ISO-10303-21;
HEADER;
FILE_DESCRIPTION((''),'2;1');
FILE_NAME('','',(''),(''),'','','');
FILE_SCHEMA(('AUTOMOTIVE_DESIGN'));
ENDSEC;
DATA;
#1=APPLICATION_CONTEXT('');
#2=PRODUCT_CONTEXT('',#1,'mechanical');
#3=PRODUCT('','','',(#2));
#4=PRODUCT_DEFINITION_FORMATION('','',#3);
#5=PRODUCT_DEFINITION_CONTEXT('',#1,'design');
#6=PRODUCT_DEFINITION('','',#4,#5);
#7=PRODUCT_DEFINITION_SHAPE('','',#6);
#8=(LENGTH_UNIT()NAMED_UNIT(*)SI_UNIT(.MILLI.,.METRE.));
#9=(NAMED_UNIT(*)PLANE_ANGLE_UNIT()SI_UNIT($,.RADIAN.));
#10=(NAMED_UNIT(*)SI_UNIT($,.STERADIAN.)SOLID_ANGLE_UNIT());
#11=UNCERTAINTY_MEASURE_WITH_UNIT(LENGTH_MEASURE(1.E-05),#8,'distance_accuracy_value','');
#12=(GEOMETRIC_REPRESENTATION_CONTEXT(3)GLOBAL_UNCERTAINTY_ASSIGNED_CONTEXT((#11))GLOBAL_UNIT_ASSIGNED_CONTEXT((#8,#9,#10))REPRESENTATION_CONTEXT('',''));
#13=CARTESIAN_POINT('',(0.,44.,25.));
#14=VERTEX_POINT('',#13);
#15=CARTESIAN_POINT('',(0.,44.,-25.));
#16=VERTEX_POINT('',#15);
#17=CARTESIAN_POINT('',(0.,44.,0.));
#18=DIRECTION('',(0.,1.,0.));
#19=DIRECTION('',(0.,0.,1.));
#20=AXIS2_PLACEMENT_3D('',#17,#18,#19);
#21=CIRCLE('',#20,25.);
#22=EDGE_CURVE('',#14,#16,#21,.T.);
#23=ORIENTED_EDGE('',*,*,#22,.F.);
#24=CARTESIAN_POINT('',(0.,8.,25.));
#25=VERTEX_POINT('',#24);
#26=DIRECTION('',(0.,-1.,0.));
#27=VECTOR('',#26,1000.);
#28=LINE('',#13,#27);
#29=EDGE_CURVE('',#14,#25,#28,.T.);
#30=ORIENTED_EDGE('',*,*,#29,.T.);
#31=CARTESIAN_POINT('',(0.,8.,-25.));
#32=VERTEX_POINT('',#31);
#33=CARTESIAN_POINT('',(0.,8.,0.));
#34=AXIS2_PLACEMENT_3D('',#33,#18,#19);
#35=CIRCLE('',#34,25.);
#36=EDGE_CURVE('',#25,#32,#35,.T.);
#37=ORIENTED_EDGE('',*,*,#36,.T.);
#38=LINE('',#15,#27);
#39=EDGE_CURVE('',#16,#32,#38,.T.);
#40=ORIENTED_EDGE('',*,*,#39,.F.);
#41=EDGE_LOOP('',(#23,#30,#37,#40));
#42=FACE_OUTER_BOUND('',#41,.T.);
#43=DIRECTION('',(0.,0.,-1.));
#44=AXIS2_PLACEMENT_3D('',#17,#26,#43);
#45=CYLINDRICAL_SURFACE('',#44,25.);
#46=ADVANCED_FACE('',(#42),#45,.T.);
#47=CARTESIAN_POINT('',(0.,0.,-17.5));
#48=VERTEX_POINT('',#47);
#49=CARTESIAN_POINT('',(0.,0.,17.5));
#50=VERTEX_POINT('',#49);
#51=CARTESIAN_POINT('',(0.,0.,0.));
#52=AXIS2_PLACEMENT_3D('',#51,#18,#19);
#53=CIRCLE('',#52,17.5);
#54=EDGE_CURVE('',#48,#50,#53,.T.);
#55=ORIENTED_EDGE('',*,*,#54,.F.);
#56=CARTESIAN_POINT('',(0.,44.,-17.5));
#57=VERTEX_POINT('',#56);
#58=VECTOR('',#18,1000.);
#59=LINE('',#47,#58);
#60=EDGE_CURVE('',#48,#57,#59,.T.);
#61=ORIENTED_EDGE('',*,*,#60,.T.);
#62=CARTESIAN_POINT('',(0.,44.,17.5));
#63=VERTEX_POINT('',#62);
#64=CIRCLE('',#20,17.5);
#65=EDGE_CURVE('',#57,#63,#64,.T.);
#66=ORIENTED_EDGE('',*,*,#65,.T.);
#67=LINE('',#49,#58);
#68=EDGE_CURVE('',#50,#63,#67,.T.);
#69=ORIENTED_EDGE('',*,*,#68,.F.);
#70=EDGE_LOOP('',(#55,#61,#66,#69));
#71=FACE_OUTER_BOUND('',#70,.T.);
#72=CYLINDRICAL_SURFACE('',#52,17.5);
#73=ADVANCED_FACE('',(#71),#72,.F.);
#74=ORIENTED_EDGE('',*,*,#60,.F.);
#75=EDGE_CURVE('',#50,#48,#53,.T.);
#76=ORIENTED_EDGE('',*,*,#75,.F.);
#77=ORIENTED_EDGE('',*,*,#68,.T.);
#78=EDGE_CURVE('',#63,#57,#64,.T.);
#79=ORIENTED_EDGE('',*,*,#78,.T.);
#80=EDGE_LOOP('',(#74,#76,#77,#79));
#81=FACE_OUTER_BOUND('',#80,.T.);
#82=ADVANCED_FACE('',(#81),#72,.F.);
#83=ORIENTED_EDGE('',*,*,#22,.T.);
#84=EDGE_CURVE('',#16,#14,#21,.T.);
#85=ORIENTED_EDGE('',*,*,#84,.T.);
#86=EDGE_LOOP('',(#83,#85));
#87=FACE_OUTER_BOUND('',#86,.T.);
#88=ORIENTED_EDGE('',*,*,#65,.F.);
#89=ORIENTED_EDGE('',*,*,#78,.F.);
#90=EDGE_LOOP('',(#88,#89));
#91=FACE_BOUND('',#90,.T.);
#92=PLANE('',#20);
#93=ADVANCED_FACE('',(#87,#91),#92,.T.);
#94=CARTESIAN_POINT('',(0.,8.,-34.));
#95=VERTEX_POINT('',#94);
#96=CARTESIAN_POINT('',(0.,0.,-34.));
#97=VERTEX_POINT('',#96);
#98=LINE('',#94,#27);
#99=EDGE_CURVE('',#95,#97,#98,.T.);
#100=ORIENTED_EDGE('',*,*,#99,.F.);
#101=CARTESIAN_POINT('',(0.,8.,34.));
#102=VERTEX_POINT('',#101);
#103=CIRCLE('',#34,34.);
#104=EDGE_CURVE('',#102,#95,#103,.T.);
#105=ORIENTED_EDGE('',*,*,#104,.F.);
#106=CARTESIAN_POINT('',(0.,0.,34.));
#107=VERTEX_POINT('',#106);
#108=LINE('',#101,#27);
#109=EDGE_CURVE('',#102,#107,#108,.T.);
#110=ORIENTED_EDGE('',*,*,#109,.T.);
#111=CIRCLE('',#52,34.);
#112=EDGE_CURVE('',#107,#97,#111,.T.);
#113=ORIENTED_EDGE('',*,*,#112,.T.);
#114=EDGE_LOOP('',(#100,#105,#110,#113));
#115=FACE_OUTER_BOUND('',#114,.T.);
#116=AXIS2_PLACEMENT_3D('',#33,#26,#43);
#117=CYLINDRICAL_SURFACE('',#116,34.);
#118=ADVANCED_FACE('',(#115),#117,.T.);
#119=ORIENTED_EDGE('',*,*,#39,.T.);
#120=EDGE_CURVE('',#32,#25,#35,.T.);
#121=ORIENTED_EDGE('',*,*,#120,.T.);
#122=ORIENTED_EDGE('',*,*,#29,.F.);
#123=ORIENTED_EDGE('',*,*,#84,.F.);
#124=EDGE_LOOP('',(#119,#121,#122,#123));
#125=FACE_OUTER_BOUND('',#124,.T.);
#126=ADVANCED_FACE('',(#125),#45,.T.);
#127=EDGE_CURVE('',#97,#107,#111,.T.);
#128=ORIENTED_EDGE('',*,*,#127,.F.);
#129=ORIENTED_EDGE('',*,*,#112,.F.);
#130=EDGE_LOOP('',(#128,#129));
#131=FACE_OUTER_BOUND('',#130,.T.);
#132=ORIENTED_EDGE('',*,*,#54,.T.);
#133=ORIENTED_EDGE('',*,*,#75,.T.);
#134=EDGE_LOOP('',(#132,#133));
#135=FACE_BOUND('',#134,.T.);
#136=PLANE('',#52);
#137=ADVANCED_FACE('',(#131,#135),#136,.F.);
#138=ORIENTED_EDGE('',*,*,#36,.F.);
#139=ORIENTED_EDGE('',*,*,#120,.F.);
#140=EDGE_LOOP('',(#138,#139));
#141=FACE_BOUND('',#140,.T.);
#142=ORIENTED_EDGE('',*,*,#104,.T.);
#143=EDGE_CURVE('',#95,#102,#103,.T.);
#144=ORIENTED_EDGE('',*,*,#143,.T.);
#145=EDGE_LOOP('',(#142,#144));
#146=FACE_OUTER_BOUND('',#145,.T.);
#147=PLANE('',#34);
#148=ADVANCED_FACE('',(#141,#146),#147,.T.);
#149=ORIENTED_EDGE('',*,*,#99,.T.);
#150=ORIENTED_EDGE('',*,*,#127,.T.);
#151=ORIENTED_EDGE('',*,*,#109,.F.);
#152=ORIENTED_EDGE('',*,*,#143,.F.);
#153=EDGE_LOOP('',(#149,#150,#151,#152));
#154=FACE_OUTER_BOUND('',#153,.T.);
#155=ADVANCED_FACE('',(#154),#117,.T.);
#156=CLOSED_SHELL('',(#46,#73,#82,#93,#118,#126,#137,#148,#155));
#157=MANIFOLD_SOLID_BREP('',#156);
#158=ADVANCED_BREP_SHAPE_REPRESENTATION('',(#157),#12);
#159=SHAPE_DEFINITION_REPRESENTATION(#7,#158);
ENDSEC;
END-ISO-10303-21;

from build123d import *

# Parameters (mm, degrees)
SKETCH1_R           = 34
BOSS_EXTRUDE1_DEPTH = 8
SKETCH2_R           = 25
BOSS_EXTRUDE2_DEPTH = 36
SKETCH3_R           = 17.5
CUT_EXTRUDE1_DEPTH  = 66.176682947


with BuildPart() as part:
    # Sketch1 → Boss-Extrude1 (new body)
    with BuildSketch(Plane(origin=(0, 0, 0), x_dir=(1, 0, 0), z_dir=(0, 1, 0))):
        with Locations(Location((0, 0, 0), (0, 0, 270))):
            Circle(SKETCH1_R)
    extrude(amount=BOSS_EXTRUDE1_DEPTH)

    # Sketch2 → Boss-Extrude2 (add)
    with BuildSketch(Plane(origin=(0, 8, 0), x_dir=(1, 0, 0), z_dir=(0, 1, 0))):
        with Locations(Location((0, 0, 0), (0, 0, 270))):
            Circle(SKETCH2_R)
    extrude(amount=BOSS_EXTRUDE2_DEPTH)

    # Sketch3 → Cut-Extrude1 (cut, through all)
    with BuildSketch(Plane(origin=(0, 44, 0), x_dir=(1, 0, 0), z_dir=(0, 1, 0))):
        with Locations(Location((0, 0, 0), (0, 0, 270))):
            Circle(SKETCH3_R)
    extrude(amount=-CUT_EXTRUDE1_DEPTH, mode=Mode.SUBTRACT)


solid = part.part
